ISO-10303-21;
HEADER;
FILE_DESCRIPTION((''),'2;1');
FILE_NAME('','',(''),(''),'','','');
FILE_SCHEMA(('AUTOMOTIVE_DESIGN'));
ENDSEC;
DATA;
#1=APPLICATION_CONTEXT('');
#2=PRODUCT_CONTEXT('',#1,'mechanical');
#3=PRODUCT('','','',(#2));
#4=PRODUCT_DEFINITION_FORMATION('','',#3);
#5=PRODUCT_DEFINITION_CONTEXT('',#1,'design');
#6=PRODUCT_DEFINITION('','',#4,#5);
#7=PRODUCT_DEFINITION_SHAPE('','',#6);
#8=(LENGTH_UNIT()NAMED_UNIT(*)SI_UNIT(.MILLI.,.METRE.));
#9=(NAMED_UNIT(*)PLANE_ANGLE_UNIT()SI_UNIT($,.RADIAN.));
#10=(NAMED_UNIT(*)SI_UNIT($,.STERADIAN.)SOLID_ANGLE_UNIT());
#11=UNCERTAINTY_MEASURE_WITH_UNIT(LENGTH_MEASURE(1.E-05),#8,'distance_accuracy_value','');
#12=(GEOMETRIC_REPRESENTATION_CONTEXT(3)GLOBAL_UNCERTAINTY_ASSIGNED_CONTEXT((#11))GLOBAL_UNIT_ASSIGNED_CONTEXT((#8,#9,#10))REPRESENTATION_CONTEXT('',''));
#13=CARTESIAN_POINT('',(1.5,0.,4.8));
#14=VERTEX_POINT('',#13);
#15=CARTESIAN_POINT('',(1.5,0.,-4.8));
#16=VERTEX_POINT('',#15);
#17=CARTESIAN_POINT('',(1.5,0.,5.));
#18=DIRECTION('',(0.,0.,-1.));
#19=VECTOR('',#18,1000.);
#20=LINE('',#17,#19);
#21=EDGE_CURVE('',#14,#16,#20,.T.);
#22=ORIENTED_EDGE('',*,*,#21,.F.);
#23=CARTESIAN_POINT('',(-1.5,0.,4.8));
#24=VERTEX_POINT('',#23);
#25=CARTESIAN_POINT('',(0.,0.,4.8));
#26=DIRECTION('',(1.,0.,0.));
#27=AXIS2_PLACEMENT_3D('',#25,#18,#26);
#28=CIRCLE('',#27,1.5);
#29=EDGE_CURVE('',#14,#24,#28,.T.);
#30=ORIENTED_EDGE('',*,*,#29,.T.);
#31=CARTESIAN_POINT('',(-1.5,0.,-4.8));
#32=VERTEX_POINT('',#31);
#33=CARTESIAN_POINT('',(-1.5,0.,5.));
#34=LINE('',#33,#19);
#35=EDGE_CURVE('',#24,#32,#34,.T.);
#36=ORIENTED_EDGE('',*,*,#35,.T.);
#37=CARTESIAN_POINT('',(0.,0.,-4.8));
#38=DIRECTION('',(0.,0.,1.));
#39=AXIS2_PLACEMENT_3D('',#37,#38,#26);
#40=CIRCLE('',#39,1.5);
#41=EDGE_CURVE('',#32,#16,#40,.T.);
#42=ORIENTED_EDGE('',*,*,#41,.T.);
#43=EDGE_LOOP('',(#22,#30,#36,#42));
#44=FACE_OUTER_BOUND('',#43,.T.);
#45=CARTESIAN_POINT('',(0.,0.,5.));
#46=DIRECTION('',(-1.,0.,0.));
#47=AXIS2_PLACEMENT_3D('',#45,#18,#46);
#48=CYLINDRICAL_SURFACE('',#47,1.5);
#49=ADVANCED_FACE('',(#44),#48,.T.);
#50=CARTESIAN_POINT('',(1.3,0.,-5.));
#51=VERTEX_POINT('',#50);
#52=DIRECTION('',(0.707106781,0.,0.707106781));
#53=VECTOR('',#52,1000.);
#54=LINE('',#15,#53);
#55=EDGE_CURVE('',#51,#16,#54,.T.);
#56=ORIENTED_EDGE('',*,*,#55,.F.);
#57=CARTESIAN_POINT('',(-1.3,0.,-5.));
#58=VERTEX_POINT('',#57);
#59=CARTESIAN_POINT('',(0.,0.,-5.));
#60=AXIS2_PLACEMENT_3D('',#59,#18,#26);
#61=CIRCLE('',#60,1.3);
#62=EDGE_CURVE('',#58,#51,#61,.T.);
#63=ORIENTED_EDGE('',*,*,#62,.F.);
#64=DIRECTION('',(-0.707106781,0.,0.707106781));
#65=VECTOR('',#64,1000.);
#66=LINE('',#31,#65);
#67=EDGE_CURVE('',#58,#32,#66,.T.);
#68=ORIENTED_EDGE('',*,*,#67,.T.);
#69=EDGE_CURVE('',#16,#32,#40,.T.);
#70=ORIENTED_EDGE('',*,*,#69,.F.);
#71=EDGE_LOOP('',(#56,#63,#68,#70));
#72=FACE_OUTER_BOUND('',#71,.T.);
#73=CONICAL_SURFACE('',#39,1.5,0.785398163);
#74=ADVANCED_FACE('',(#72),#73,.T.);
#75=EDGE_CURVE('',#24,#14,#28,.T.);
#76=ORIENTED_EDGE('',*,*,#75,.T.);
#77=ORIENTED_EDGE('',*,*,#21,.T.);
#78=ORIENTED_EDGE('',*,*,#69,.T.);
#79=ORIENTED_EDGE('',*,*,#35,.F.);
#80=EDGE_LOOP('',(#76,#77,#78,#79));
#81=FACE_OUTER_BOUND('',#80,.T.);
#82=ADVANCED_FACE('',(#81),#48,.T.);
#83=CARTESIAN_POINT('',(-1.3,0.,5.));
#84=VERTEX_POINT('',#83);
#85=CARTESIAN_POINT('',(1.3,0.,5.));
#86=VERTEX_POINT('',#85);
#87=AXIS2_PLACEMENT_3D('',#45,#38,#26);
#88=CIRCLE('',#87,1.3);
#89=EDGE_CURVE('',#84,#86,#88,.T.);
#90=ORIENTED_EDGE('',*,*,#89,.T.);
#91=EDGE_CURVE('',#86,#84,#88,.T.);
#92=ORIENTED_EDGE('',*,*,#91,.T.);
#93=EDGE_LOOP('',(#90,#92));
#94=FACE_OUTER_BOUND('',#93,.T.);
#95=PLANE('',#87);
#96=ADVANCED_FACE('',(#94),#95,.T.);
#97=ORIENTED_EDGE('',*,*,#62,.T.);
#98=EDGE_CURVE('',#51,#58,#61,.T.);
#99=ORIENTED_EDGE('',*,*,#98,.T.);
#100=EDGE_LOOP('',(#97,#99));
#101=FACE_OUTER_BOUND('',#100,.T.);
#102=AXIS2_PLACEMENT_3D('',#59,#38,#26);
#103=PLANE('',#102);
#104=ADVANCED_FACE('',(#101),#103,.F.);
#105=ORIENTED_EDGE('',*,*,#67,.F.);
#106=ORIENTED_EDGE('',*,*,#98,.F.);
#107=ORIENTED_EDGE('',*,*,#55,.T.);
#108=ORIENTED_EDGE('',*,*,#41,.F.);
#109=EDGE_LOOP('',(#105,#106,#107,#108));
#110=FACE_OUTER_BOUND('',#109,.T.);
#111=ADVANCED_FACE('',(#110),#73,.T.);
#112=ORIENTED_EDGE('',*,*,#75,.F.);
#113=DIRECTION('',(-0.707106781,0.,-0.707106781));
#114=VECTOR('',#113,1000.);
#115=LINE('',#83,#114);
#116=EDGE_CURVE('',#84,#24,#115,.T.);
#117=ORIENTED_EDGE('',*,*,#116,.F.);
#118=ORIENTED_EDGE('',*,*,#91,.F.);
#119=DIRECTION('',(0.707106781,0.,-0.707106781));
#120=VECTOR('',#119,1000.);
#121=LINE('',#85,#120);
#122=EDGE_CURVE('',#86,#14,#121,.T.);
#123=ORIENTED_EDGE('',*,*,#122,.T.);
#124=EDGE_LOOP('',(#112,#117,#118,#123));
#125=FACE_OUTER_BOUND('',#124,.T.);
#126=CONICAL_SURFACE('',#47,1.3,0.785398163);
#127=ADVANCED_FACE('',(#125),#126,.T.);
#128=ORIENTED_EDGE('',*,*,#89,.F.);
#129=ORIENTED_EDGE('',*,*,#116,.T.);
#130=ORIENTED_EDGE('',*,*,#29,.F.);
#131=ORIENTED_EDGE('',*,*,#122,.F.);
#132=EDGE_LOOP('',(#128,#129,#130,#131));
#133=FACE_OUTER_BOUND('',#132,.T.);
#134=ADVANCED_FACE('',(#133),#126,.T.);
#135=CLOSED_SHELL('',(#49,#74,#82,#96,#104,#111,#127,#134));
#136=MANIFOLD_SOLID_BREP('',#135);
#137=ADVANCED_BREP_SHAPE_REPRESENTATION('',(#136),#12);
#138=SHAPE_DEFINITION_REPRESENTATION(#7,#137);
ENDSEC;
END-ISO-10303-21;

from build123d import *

# Parameters (mm, degrees)
PIN_PROFILE_3_R          = 1.5
PIN_BODY_3X10_DEPTH      = 5
END_CHAMFERS_0_2X45_SIZE = 0.2


with BuildPart() as part:
    # Pin Profile Ø3 → Pin Body Ø3x10 (new, symmetric)
    with BuildSketch(Plane.XY):
        Circle(PIN_PROFILE_3_R)
    extrude(amount=PIN_BODY_3X10_DEPTH, both=True)

    # End Chamfers 0.2x45°
    end_chamfers_0_2x45_edges = [part.edges().sort_by_distance(p)[0] for p in [
        (-1.5, 0, -5),
        (-1.5, 0, 5),
    ]]
    chamfer(end_chamfers_0_2x45_edges, length=END_CHAMFERS_0_2X45_SIZE)


solid = part.part
